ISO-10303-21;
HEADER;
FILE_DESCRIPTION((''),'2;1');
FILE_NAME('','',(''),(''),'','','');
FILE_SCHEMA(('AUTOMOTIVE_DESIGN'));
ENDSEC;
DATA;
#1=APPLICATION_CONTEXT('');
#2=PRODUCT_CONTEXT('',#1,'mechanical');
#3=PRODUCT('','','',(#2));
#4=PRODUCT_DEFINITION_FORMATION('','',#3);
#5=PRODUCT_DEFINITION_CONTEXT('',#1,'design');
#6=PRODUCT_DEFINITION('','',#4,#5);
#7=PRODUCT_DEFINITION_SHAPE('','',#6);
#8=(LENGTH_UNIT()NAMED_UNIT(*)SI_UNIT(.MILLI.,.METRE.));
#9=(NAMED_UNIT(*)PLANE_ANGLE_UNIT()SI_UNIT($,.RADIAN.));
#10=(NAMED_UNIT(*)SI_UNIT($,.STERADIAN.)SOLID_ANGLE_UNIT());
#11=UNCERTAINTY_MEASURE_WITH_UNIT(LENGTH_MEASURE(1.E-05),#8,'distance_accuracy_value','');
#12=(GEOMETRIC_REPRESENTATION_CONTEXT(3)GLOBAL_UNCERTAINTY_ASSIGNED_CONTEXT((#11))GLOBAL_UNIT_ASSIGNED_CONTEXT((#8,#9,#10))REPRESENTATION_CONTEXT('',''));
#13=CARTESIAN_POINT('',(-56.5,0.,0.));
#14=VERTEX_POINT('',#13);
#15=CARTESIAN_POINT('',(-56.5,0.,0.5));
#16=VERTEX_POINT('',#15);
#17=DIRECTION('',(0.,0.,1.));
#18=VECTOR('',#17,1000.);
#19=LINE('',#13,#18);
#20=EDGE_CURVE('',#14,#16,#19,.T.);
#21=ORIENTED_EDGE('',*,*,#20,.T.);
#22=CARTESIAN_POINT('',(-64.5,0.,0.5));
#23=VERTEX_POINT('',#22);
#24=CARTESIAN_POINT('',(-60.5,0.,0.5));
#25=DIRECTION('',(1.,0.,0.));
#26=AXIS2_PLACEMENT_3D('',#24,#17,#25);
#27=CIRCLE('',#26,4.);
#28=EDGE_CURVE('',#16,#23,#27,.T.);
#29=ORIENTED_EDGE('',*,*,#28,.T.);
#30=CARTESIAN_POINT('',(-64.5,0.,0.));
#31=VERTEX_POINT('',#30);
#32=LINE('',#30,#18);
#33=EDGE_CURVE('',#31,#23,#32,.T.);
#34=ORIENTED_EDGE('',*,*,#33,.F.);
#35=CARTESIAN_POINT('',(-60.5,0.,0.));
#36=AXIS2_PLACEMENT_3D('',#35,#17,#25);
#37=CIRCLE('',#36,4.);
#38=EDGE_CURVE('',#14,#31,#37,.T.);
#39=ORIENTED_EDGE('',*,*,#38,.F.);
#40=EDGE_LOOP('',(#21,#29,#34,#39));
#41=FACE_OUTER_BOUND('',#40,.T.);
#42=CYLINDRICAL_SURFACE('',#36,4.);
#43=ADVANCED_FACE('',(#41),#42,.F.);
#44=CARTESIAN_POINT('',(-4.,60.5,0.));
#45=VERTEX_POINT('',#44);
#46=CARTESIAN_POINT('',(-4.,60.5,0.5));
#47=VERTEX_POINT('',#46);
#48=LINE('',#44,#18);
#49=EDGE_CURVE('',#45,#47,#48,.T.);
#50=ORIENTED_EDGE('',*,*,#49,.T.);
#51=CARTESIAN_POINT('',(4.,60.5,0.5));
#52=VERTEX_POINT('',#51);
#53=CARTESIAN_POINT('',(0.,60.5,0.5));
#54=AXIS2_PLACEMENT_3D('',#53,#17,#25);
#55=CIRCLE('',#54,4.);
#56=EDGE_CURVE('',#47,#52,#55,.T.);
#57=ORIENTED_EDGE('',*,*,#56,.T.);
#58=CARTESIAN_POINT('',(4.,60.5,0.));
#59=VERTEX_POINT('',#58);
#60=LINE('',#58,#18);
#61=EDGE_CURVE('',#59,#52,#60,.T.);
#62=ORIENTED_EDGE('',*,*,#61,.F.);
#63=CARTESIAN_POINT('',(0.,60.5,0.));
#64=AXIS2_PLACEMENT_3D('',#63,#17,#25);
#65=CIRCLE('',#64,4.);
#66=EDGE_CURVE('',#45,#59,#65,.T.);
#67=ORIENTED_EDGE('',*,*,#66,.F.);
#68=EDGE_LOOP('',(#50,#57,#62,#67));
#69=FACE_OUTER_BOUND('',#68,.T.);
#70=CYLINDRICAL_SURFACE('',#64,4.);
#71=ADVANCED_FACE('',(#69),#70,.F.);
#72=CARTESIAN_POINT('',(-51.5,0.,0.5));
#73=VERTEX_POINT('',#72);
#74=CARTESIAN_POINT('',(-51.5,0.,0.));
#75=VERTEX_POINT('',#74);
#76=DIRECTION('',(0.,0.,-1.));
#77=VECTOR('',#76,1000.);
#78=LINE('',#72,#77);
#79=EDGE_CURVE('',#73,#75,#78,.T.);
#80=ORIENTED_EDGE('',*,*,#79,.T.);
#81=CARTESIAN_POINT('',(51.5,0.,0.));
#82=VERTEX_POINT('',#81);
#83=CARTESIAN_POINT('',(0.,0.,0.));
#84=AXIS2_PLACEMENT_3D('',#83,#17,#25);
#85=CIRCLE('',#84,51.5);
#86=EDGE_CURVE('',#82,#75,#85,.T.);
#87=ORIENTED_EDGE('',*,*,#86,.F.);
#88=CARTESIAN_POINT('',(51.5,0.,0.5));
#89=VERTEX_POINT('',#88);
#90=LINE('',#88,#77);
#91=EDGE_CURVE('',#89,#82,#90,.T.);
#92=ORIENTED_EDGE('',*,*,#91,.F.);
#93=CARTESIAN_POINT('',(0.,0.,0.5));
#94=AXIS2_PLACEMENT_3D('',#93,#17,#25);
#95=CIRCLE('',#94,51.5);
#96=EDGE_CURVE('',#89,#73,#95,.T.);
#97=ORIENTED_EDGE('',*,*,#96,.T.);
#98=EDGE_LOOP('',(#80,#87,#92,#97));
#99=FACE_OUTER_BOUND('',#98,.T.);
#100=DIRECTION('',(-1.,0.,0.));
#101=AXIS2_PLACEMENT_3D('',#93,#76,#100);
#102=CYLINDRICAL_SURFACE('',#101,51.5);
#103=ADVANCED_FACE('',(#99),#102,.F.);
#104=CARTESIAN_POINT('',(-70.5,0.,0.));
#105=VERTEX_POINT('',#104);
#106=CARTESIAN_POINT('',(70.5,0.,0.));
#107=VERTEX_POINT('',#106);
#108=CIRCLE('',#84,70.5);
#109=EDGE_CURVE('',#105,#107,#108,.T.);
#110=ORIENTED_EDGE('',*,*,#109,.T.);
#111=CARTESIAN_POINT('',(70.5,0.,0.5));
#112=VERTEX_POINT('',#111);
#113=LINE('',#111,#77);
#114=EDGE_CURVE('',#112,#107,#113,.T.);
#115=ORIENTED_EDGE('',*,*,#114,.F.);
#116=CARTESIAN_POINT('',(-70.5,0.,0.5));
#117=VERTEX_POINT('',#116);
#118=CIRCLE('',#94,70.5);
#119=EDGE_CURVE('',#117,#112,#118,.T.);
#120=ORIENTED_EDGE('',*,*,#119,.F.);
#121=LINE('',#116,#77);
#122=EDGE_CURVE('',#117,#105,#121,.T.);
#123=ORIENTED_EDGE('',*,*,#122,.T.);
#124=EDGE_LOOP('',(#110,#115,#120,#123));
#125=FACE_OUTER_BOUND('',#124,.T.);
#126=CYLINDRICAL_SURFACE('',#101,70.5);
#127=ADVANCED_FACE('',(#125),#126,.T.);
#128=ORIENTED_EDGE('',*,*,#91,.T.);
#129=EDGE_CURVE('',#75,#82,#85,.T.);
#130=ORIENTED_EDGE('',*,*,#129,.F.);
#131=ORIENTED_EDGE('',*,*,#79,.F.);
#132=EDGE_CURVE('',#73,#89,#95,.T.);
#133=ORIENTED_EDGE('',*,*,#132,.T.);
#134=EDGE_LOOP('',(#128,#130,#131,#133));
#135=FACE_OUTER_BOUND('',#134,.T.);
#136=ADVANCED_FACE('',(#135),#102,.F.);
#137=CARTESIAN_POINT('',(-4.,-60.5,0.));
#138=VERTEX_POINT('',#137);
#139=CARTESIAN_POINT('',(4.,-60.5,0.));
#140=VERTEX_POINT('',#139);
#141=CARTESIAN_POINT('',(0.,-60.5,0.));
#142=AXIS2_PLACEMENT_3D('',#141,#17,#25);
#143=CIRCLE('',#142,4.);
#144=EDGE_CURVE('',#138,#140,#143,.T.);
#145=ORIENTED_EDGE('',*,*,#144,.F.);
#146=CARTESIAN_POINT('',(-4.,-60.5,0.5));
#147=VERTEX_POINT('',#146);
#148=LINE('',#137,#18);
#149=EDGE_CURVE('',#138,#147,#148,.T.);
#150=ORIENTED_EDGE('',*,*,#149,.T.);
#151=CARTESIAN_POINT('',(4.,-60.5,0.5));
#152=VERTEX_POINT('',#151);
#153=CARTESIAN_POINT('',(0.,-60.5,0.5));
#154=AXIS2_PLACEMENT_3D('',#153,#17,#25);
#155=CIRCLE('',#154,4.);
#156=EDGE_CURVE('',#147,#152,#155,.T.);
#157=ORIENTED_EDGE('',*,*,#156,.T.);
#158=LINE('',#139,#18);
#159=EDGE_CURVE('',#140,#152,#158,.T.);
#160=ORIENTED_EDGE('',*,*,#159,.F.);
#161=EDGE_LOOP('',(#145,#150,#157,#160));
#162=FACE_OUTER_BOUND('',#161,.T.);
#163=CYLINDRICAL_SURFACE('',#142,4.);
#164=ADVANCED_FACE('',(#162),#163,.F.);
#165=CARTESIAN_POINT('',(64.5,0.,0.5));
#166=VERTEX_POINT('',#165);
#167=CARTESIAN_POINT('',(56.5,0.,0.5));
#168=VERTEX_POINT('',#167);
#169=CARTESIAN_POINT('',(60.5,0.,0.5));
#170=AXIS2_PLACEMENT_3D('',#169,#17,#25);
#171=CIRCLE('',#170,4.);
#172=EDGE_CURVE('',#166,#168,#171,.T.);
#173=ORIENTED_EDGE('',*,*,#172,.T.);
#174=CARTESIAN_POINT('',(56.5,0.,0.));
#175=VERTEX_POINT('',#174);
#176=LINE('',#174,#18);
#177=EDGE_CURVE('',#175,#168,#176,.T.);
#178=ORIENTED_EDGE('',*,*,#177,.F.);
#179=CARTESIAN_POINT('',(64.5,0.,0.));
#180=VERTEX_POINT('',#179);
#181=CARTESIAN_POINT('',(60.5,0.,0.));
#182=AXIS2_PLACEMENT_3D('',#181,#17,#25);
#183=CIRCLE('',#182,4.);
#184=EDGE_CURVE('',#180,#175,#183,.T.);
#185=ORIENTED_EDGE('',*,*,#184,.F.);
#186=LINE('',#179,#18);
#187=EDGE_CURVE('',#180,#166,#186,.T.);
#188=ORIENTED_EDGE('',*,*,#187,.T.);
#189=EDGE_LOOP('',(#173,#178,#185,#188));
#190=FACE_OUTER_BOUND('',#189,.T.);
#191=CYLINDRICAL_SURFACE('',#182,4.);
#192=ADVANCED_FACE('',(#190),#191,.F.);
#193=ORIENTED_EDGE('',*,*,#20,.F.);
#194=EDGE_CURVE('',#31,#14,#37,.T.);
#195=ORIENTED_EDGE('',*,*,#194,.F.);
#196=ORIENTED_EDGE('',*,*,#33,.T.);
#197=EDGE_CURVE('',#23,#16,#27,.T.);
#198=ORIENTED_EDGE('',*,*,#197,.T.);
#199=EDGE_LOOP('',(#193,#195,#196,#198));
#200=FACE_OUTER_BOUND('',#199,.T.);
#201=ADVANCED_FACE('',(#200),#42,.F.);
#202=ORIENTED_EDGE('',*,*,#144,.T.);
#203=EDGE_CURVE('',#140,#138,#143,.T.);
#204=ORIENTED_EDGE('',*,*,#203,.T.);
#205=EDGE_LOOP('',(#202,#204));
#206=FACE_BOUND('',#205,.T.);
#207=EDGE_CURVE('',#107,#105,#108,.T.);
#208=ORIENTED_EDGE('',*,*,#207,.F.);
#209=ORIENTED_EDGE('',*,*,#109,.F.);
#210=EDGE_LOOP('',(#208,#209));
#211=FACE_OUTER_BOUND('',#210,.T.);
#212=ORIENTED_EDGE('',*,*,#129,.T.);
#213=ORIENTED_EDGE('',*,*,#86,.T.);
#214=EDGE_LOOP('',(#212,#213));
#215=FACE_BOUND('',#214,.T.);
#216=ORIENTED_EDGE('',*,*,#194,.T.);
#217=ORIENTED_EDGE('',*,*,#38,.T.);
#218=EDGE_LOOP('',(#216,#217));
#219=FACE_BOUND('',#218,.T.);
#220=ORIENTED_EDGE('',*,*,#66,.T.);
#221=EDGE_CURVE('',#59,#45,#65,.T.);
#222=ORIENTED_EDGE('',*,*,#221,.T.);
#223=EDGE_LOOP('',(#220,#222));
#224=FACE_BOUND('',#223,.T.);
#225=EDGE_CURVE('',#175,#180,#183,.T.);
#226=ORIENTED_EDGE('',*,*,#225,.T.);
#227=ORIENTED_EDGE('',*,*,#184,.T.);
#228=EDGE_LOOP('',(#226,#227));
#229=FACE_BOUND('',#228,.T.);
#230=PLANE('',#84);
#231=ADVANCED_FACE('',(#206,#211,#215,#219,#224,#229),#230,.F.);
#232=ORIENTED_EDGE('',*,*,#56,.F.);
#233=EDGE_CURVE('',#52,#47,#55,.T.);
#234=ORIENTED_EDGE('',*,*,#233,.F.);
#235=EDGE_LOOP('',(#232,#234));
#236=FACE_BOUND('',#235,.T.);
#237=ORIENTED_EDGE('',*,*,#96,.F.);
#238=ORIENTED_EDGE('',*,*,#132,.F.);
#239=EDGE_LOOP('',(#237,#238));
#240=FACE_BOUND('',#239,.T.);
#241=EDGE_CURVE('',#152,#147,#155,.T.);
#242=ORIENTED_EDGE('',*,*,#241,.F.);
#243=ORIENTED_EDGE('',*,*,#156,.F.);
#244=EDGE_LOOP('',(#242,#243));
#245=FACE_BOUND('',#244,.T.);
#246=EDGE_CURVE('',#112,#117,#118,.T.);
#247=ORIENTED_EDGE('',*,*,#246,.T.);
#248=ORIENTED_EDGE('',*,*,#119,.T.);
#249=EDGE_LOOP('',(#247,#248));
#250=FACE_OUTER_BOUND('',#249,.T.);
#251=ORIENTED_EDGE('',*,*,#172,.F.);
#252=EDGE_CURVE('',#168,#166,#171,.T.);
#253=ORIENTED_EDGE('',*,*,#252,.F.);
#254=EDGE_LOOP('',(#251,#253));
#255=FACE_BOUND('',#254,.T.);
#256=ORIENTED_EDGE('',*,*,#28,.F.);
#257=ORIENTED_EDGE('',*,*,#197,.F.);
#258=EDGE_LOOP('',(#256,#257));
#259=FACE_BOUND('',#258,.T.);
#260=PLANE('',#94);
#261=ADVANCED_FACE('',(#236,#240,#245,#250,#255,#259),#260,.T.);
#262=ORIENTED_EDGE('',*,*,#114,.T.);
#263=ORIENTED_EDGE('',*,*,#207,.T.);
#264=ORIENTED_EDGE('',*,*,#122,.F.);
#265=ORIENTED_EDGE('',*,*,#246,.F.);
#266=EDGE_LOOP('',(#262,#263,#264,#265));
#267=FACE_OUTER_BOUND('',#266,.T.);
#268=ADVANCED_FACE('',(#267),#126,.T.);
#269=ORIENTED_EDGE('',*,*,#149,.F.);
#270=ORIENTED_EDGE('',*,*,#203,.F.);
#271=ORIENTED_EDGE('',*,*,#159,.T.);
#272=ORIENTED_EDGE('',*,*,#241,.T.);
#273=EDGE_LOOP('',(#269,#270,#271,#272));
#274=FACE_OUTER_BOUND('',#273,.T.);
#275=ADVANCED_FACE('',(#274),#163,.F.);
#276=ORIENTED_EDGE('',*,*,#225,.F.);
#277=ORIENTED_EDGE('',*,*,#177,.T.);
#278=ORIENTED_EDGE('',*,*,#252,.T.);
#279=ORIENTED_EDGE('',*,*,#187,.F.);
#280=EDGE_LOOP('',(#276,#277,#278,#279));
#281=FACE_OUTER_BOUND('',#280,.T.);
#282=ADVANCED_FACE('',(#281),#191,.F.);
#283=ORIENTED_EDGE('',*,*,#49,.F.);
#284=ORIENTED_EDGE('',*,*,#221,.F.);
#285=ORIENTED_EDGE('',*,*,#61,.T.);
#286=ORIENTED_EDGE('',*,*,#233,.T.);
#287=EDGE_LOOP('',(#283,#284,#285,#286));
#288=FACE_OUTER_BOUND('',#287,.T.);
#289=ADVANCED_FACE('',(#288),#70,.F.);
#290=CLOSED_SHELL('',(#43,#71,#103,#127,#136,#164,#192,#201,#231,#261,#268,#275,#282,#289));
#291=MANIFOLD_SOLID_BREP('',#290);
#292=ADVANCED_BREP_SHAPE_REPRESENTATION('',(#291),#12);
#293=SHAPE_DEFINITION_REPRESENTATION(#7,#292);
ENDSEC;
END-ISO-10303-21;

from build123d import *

# Parameters (mm, degrees)
SKETCH1_R           = 70.5
SKETCH1_R_2         = 51.5
BOSS_EXTRUDE1_DEPTH = 0.5
SKETCH2_R           = 4
CUT_EXTRUDE1_DEPTH  = 0.5


with BuildPart() as part:
    # Sketch1 → Boss-Extrude1 (new body)
    with BuildSketch(Plane.XY):
        Circle(SKETCH1_R)
        Circle(SKETCH1_R_2, mode=Mode.SUBTRACT)
    extrude(amount=BOSS_EXTRUDE1_DEPTH)

    # Sketch2 → Cut-Extrude1 (cut)
    with BuildSketch(Plane.XY.offset(0.5)):
        with Locations((0, -60.5)):
            Circle(SKETCH2_R)
        with Locations((-60.5, 0)):
            Circle(SKETCH2_R)
        with Locations((0, 60.5)):
            Circle(SKETCH2_R)
        with Locations((60.5, 0)):
            Circle(SKETCH2_R)
    extrude(amount=-CUT_EXTRUDE1_DEPTH, mode=Mode.SUBTRACT)


solid = part.part
